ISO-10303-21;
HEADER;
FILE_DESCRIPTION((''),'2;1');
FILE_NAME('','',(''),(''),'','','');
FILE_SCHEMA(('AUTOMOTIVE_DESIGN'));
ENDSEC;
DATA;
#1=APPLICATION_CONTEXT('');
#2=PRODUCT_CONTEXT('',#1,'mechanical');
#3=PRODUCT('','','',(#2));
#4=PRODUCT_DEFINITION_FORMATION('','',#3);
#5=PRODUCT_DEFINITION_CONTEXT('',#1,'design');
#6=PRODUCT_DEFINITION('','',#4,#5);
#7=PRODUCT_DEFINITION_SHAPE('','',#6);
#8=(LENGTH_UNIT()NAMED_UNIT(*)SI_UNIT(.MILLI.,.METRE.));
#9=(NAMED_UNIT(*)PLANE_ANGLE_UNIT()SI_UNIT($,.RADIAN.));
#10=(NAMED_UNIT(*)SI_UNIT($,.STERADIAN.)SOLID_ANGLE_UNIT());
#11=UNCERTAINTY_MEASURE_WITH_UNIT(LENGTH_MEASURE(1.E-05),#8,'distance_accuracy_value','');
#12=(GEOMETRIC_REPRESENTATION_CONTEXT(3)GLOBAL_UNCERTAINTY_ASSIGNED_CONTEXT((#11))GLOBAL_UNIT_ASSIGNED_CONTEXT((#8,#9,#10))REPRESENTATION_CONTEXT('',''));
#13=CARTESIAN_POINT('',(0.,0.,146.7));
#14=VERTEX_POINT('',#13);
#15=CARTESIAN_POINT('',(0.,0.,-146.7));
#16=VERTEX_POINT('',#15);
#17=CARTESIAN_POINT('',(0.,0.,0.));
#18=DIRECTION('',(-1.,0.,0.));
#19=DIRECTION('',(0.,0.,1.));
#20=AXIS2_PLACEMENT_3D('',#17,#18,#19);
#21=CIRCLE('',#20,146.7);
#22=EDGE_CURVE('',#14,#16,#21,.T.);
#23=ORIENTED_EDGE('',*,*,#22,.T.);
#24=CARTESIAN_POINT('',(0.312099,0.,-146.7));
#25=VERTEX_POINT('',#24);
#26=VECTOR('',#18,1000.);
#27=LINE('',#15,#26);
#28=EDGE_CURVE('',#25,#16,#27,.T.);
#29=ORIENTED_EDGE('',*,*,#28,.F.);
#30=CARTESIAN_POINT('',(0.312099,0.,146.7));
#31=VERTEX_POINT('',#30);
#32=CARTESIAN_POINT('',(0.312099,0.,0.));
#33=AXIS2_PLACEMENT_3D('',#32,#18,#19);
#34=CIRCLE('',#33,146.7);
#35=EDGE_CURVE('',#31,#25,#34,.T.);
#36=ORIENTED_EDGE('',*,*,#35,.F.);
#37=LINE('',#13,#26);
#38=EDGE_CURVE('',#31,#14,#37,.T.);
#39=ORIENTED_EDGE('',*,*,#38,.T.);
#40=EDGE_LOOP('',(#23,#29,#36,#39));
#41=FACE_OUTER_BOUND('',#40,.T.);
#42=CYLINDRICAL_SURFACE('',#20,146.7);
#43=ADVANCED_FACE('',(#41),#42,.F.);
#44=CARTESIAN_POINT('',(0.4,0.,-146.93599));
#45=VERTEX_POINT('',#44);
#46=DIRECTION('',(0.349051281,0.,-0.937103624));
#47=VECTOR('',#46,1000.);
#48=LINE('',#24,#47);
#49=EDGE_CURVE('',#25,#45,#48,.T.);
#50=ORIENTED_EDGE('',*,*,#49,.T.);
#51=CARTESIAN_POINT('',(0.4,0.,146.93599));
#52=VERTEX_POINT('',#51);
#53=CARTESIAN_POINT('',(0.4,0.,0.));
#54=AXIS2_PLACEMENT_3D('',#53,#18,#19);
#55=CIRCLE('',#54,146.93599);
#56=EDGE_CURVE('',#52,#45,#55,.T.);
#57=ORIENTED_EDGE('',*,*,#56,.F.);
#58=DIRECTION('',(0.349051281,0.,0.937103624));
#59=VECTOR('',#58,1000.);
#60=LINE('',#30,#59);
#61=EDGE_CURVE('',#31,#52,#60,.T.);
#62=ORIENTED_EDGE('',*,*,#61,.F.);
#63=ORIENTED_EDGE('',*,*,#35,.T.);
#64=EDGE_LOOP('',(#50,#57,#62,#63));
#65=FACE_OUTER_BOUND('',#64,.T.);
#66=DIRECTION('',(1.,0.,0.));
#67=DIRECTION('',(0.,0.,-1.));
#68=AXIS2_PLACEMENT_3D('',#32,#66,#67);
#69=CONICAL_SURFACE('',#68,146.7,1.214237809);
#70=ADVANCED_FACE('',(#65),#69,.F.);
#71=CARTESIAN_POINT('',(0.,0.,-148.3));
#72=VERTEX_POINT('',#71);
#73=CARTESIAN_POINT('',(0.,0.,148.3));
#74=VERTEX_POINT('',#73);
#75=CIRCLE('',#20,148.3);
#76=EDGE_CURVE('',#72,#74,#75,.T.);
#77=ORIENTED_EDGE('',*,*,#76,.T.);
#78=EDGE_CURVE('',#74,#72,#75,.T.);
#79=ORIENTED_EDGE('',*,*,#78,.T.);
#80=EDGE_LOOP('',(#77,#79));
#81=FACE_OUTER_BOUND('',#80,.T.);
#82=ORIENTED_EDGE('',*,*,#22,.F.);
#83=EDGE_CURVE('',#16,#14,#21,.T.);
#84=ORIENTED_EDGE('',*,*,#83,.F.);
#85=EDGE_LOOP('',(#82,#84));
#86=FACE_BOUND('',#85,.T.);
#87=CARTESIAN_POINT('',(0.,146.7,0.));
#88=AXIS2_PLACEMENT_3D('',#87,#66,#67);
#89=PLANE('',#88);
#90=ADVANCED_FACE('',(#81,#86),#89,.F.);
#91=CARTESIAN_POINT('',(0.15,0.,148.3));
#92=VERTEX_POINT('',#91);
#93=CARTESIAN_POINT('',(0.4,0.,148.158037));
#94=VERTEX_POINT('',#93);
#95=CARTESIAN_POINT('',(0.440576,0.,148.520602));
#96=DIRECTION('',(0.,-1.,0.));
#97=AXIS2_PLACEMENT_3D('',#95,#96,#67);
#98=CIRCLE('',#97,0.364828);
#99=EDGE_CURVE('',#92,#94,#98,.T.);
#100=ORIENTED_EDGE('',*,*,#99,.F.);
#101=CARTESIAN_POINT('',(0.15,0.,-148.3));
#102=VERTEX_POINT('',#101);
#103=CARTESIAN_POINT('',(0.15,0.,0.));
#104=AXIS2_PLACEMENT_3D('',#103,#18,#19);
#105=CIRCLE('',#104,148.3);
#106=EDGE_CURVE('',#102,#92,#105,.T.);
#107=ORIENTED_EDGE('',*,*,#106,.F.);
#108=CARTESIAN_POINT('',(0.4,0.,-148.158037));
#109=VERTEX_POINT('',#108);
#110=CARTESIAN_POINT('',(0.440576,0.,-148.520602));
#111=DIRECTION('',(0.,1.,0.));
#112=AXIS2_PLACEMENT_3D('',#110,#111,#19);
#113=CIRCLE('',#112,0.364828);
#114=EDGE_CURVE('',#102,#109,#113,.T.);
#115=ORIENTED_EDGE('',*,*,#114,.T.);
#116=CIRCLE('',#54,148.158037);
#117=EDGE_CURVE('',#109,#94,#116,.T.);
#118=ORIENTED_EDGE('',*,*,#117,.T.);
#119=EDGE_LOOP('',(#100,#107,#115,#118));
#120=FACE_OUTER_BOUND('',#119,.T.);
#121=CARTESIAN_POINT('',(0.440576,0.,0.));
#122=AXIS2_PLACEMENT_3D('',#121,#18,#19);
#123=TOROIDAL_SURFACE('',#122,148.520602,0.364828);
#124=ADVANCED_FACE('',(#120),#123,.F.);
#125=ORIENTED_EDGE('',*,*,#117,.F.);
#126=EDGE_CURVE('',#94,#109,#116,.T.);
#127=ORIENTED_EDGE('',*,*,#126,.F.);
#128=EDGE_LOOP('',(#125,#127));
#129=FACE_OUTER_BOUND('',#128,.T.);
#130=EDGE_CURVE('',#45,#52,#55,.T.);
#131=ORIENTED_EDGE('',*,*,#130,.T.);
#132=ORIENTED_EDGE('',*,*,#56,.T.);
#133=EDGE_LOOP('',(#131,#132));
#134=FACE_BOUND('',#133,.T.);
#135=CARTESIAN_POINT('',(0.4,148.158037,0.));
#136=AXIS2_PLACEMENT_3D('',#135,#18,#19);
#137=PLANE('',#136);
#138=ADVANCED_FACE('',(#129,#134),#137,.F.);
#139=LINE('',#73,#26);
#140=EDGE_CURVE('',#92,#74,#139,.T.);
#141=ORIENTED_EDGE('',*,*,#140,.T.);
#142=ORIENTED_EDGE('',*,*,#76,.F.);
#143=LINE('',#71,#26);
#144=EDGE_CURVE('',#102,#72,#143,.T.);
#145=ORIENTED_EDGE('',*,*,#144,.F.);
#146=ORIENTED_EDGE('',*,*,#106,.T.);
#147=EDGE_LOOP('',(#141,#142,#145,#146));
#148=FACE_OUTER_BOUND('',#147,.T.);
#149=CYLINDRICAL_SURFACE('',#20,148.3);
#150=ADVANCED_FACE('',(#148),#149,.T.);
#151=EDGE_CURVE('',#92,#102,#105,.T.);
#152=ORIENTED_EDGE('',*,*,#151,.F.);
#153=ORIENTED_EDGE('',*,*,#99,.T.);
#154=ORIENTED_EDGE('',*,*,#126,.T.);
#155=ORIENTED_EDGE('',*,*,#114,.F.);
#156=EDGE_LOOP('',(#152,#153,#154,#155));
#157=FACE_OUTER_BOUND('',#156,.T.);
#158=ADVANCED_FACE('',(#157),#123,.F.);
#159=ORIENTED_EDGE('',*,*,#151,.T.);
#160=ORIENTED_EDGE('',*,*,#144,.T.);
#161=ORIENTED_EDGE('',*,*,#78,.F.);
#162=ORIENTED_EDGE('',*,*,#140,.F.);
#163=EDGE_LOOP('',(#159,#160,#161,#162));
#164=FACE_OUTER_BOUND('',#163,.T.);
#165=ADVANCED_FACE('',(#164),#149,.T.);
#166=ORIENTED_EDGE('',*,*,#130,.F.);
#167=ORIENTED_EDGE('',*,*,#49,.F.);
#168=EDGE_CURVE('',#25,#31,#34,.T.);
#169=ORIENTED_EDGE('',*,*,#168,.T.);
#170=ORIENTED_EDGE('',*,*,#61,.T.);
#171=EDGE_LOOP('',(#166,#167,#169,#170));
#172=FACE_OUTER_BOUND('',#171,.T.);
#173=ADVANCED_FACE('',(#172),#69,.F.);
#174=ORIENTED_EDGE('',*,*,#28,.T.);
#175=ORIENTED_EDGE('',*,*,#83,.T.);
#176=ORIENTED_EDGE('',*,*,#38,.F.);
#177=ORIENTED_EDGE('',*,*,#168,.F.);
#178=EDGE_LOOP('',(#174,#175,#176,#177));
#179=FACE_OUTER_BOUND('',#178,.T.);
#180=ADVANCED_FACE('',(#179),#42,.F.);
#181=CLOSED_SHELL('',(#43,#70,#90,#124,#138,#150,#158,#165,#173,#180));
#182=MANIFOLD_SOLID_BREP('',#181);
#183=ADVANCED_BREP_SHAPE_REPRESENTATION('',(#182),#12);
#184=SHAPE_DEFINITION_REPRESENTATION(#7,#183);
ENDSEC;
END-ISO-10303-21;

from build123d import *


with BuildPart() as part:
    # 草图1 → 旋转1 (revolve)
    with BuildSketch(Plane.XY, mode=Mode.PRIVATE) as revolve_1_sk:
        with BuildLine():
            Line((0, 148.3), (0.15, 148.3))
            ThreePointArc((0.15, 148.3), (0.260426662, 148.203354538), (0.4, 148.158037035))
            Line((0.4, 148.158037035), (0.4, 146.935990161))
            Line((0.4, 146.935990161), (0.312098656, 146.7))
            Line((0.312098656, 146.7), (0, 146.7))
            Line((0, 146.7), (0, 148.3))
        make_face()
    revolve(revolve_1_sk.sketch.rotate(Axis((0, 0, 0), (1, 0, 0)), 90), axis=Axis((0, 0, 0), (1, 0, 0)))


solid = part.part
